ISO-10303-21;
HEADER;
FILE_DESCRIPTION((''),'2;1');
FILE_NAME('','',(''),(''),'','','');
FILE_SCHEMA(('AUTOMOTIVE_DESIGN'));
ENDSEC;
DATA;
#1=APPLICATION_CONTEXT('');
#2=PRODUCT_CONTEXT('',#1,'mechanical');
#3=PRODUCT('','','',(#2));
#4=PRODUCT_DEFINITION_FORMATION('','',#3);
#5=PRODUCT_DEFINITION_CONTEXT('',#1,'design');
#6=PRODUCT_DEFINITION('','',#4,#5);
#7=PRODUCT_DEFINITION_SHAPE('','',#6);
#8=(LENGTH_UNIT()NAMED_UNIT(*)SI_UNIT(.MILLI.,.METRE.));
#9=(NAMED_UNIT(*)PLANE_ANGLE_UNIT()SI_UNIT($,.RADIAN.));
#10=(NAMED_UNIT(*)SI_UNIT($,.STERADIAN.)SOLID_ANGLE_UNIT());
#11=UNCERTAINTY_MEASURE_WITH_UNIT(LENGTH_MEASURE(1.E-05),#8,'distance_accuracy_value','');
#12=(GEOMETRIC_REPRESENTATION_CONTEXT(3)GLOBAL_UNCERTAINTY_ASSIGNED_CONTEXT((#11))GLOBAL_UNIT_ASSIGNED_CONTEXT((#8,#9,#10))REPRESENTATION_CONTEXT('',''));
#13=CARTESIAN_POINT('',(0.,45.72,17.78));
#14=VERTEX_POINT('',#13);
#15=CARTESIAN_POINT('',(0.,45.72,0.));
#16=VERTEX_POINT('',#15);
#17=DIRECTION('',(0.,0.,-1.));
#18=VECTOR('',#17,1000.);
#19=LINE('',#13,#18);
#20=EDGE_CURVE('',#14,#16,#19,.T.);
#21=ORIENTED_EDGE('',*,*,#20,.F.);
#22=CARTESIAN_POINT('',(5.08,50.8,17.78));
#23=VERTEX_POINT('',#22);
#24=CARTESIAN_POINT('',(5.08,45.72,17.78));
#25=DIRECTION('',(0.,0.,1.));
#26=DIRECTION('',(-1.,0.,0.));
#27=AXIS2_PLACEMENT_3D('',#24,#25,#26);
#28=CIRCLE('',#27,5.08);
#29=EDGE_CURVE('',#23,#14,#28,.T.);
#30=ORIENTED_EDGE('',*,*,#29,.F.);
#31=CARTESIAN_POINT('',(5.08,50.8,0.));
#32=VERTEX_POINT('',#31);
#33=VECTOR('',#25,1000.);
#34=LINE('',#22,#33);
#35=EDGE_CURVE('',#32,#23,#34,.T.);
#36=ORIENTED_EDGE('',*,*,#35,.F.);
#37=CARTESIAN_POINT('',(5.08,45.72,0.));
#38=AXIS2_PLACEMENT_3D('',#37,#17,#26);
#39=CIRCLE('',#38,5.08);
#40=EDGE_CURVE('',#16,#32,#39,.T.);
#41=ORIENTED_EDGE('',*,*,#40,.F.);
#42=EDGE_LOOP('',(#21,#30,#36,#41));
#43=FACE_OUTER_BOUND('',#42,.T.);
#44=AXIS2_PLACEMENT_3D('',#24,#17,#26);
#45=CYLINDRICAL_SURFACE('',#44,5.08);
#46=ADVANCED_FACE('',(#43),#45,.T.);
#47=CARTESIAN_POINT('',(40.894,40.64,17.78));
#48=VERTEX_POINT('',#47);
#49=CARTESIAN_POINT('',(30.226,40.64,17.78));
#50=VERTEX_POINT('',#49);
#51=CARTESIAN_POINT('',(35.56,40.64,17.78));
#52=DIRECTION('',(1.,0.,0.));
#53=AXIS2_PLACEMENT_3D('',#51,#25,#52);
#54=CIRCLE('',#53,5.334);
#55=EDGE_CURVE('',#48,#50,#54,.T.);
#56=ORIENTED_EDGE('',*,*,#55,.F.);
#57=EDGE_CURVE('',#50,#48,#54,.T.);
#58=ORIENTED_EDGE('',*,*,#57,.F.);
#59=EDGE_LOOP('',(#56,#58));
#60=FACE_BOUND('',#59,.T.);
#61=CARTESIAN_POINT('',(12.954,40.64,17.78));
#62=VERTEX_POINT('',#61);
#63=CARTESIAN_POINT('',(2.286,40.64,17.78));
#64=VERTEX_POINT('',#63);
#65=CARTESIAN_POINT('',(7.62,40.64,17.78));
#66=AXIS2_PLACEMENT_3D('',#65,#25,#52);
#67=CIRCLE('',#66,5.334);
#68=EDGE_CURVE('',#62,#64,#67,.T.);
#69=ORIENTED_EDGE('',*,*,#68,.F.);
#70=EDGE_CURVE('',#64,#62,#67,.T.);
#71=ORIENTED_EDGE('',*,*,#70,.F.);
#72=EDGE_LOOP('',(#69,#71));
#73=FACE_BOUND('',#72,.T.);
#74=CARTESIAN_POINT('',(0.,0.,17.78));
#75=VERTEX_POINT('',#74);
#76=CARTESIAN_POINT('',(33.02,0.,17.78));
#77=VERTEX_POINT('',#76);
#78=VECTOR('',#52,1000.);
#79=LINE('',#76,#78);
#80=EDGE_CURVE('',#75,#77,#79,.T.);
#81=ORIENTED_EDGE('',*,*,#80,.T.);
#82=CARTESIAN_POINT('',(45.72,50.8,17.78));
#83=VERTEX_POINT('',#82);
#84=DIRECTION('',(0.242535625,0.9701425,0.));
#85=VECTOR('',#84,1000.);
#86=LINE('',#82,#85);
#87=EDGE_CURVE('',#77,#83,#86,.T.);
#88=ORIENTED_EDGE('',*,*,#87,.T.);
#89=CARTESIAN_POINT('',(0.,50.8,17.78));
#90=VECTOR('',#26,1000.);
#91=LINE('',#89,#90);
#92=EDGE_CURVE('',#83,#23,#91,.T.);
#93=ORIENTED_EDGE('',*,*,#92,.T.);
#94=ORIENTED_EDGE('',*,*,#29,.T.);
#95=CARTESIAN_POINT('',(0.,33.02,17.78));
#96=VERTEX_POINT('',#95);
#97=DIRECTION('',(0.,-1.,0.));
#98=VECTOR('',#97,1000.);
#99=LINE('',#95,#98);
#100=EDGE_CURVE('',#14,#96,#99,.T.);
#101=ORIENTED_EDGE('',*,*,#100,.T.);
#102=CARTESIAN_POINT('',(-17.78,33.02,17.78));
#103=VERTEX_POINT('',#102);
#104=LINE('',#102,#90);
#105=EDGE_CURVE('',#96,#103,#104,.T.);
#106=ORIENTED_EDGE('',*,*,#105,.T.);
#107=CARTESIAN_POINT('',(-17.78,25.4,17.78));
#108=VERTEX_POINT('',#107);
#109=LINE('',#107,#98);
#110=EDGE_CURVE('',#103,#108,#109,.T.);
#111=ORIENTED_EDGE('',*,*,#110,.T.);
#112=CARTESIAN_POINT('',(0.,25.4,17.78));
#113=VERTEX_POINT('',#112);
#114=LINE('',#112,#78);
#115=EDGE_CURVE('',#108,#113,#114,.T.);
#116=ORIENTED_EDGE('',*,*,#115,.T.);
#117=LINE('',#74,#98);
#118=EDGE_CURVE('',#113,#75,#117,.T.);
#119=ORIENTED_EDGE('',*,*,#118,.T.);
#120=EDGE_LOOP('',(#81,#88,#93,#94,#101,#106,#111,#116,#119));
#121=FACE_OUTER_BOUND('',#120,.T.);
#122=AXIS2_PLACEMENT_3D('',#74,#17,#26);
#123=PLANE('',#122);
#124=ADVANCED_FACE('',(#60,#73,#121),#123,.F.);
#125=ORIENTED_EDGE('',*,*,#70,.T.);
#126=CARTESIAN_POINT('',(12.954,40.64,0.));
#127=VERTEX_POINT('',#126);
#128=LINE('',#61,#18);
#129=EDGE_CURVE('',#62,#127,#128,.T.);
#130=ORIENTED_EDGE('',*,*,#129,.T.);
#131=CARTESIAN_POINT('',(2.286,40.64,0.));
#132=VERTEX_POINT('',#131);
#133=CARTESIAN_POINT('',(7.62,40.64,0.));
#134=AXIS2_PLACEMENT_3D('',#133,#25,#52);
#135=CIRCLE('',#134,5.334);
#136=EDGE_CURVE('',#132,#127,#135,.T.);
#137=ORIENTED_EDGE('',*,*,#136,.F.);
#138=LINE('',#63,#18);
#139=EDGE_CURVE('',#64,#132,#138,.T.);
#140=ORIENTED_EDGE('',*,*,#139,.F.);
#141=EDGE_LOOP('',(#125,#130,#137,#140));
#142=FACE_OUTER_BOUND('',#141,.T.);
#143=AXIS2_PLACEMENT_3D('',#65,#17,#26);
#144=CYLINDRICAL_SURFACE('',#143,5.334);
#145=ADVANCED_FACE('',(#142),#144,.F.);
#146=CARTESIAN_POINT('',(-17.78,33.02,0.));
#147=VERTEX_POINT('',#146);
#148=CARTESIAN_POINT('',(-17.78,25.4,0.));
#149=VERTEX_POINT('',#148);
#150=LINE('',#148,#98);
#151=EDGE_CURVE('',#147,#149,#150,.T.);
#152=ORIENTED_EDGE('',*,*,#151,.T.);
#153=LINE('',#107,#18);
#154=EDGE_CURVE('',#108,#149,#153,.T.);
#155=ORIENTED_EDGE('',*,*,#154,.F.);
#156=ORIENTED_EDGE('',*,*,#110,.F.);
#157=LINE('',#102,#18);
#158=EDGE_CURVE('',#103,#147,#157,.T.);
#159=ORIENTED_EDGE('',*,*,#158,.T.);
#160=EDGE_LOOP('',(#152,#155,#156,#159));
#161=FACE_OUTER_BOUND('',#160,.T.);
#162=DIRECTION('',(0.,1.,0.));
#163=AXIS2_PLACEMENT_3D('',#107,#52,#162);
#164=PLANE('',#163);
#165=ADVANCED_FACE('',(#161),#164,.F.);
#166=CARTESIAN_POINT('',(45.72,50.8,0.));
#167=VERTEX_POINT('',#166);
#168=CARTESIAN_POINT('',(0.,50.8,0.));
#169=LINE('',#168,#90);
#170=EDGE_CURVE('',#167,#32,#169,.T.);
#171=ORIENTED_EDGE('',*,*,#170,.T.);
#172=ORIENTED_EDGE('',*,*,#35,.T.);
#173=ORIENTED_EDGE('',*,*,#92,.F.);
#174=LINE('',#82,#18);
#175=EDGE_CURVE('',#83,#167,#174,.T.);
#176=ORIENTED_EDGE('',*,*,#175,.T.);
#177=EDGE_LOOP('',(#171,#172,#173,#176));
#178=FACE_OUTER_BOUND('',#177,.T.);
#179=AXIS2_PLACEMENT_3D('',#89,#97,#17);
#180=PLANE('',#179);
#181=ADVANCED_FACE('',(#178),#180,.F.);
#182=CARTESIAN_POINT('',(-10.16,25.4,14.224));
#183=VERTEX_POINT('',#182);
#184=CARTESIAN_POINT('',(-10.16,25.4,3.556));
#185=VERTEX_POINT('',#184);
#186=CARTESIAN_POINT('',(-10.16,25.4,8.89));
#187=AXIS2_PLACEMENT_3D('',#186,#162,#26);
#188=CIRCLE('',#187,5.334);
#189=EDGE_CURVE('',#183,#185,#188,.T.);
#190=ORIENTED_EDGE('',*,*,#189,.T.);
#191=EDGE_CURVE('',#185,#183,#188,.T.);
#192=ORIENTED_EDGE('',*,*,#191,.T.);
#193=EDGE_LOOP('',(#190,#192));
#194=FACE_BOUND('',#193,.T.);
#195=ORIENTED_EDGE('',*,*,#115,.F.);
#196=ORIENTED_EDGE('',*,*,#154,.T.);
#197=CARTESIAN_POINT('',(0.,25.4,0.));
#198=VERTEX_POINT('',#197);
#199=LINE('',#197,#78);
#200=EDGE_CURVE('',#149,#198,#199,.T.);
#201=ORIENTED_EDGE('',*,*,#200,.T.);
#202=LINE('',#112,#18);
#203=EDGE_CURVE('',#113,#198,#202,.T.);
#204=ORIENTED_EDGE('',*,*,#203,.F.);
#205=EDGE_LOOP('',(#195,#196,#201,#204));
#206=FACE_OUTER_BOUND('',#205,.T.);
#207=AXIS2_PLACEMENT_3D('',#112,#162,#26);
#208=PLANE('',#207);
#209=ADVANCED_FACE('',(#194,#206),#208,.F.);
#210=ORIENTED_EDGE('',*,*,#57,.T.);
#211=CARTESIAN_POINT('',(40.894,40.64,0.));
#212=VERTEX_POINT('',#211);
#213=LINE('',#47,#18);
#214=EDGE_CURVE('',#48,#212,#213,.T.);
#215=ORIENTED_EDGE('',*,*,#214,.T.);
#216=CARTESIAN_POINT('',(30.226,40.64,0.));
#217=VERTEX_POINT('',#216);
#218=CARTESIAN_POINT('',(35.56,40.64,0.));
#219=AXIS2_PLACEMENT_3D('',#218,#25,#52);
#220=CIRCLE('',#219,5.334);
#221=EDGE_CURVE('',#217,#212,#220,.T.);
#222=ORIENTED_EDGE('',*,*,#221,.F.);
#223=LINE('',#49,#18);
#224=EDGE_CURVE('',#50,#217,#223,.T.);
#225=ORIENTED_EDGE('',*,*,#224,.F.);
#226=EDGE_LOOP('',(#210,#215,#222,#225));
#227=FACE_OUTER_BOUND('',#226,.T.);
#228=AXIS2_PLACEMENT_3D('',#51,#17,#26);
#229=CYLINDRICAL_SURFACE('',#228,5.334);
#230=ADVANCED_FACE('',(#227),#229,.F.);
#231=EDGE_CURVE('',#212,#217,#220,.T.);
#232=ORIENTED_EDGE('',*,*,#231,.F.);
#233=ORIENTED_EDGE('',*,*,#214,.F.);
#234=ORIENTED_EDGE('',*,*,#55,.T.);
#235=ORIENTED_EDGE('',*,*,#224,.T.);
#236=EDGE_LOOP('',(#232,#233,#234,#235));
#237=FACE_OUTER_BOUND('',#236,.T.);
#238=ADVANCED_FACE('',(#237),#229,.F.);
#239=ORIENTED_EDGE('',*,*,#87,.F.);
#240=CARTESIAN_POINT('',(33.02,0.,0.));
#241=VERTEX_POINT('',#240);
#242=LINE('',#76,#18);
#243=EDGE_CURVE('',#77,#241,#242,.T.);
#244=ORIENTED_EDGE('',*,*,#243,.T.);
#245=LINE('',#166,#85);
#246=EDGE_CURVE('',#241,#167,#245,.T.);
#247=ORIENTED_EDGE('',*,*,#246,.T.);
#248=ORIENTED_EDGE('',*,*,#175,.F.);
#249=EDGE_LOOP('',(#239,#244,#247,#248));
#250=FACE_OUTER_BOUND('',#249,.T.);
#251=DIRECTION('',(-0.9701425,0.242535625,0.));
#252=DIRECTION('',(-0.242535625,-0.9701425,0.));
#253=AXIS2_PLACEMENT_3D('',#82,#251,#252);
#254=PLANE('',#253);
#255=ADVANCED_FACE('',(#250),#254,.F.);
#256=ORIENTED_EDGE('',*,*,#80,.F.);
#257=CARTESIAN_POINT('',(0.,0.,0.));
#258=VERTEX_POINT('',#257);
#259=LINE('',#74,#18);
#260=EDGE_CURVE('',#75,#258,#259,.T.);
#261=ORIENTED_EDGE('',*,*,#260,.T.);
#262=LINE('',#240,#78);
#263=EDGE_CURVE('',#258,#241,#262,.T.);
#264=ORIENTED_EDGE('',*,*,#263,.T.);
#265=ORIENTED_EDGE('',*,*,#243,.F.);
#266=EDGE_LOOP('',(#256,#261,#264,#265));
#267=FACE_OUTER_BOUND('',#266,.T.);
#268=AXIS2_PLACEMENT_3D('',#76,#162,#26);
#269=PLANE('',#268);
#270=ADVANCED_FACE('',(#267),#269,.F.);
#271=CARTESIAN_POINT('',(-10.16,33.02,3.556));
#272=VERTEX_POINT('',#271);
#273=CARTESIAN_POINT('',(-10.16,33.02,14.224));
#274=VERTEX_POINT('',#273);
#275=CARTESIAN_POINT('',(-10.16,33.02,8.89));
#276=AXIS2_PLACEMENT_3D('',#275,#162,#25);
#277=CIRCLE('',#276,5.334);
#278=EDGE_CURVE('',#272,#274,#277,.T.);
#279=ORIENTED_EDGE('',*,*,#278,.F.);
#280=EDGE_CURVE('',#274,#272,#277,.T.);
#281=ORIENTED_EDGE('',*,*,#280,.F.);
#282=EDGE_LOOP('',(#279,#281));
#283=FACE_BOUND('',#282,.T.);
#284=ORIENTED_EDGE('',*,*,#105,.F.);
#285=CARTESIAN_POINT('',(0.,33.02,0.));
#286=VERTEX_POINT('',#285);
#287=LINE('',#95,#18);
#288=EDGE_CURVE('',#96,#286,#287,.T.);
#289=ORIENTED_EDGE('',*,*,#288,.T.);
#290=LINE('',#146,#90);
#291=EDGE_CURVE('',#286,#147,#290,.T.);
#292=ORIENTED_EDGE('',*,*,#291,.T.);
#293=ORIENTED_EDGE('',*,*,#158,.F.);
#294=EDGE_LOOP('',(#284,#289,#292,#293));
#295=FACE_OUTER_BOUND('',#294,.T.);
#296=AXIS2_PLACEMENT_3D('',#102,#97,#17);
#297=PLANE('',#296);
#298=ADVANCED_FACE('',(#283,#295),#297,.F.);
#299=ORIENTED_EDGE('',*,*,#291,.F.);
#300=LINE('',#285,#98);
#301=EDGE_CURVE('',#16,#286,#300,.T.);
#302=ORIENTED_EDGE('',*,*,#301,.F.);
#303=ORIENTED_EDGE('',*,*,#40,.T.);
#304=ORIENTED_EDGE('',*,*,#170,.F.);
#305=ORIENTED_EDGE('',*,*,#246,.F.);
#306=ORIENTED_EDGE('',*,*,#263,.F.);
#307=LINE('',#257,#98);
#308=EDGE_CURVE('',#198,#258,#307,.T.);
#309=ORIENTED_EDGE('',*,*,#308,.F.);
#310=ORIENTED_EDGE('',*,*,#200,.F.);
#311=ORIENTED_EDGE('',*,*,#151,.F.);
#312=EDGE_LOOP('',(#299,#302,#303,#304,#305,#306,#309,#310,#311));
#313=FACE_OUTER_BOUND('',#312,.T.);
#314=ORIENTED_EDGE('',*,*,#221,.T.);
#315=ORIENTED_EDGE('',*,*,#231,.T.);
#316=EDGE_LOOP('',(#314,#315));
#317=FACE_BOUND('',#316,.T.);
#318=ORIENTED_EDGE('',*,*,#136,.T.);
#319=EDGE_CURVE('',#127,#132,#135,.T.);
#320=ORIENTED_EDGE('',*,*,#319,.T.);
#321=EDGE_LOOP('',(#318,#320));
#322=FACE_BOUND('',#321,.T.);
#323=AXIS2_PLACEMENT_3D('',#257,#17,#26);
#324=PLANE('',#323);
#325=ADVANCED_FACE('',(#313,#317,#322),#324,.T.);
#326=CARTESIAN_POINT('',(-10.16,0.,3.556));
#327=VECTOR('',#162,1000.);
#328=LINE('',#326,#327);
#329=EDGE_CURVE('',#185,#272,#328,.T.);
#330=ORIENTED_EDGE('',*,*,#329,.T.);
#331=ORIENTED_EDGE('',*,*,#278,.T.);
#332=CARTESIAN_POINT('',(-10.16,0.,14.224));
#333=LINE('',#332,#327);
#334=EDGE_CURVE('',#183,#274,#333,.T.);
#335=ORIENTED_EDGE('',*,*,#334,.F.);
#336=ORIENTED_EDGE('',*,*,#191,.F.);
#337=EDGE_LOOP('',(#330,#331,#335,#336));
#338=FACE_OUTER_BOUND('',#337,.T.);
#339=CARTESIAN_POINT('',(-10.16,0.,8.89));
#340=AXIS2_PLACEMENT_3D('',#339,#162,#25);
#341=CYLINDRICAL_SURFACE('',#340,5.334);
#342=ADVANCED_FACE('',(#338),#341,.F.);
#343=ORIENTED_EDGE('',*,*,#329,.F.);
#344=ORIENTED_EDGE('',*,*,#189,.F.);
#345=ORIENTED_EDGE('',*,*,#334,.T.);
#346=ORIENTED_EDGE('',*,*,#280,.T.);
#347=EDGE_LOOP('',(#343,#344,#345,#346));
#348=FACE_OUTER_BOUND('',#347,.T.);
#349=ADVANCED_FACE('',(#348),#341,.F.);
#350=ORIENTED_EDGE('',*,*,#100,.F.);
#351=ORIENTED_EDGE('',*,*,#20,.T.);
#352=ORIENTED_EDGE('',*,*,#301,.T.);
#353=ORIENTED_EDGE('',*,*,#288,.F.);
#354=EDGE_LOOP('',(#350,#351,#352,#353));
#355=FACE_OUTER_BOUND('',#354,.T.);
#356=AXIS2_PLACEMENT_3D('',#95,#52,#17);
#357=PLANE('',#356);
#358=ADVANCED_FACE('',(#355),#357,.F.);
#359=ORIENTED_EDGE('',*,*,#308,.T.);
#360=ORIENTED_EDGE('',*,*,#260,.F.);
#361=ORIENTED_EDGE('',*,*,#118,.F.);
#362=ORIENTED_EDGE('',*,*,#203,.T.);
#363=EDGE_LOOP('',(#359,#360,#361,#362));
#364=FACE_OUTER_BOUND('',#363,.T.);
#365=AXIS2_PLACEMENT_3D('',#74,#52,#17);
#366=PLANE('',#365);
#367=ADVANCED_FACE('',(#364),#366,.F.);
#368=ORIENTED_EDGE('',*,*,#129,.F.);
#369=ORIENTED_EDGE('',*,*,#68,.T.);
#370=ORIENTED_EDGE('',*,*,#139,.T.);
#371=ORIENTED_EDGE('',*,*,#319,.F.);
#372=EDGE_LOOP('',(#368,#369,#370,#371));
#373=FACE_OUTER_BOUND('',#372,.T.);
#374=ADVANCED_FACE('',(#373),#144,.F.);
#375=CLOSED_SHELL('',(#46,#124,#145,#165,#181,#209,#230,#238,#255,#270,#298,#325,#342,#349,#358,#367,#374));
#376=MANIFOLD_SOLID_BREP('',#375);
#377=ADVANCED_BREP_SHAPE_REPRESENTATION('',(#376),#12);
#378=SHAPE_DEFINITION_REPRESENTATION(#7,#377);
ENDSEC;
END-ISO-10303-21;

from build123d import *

# Parameters (mm, degrees)
SKETCH2_R           = 2.667
BOSS_EXTRUDE1_DEPTH = 8.89
SKETCH3_R           = 2.667
CUT_EXTRUDE1_DEPTH  = 30.566734686
FILLET1_R           = 2.54
SCALE1_SCALE        = 2


with BuildPart() as part:
    # Sketch2 → Boss-Extrude1 (new body)
    with BuildSketch(Plane.XY):
        Polygon((0, 0), (0, 12.7), (-8.89, 12.7), (-8.89, 16.51), (0, 16.51), (0, 25.4), (22.86, 25.4), (16.51, 0), align=None)
        with Locations((3.81, 20.32)):
            Circle(SKETCH2_R, mode=Mode.SUBTRACT)
        with Locations((17.78, 20.32)):
            Circle(SKETCH2_R, mode=Mode.SUBTRACT)
    extrude(amount=BOSS_EXTRUDE1_DEPTH)

    # Sketch3 → Cut-Extrude1 (cut, through all)
    with BuildSketch(Plane(origin=(0, 16.51, 0), x_dir=(1, 0, 0), z_dir=(0, 1, 0))):
        with Locations(Location((-5.08, -4.445, 0), (0, 0, 270))):
            Circle(SKETCH3_R)
    extrude(amount=-CUT_EXTRUDE1_DEPTH, mode=Mode.SUBTRACT)

    # Fillet1
    fillet1_edges = [part.edges().sort_by_distance(p)[0] for p in [
        (0, 25.4, 4.445),
    ]]
    fillet(fillet1_edges, radius=FILLET1_R)


with BuildPart() as part_1:
    # Scale1: scaled about (0, 0, 0)
    add(part.part.scale(SCALE1_SCALE))


solid = part_1.part
